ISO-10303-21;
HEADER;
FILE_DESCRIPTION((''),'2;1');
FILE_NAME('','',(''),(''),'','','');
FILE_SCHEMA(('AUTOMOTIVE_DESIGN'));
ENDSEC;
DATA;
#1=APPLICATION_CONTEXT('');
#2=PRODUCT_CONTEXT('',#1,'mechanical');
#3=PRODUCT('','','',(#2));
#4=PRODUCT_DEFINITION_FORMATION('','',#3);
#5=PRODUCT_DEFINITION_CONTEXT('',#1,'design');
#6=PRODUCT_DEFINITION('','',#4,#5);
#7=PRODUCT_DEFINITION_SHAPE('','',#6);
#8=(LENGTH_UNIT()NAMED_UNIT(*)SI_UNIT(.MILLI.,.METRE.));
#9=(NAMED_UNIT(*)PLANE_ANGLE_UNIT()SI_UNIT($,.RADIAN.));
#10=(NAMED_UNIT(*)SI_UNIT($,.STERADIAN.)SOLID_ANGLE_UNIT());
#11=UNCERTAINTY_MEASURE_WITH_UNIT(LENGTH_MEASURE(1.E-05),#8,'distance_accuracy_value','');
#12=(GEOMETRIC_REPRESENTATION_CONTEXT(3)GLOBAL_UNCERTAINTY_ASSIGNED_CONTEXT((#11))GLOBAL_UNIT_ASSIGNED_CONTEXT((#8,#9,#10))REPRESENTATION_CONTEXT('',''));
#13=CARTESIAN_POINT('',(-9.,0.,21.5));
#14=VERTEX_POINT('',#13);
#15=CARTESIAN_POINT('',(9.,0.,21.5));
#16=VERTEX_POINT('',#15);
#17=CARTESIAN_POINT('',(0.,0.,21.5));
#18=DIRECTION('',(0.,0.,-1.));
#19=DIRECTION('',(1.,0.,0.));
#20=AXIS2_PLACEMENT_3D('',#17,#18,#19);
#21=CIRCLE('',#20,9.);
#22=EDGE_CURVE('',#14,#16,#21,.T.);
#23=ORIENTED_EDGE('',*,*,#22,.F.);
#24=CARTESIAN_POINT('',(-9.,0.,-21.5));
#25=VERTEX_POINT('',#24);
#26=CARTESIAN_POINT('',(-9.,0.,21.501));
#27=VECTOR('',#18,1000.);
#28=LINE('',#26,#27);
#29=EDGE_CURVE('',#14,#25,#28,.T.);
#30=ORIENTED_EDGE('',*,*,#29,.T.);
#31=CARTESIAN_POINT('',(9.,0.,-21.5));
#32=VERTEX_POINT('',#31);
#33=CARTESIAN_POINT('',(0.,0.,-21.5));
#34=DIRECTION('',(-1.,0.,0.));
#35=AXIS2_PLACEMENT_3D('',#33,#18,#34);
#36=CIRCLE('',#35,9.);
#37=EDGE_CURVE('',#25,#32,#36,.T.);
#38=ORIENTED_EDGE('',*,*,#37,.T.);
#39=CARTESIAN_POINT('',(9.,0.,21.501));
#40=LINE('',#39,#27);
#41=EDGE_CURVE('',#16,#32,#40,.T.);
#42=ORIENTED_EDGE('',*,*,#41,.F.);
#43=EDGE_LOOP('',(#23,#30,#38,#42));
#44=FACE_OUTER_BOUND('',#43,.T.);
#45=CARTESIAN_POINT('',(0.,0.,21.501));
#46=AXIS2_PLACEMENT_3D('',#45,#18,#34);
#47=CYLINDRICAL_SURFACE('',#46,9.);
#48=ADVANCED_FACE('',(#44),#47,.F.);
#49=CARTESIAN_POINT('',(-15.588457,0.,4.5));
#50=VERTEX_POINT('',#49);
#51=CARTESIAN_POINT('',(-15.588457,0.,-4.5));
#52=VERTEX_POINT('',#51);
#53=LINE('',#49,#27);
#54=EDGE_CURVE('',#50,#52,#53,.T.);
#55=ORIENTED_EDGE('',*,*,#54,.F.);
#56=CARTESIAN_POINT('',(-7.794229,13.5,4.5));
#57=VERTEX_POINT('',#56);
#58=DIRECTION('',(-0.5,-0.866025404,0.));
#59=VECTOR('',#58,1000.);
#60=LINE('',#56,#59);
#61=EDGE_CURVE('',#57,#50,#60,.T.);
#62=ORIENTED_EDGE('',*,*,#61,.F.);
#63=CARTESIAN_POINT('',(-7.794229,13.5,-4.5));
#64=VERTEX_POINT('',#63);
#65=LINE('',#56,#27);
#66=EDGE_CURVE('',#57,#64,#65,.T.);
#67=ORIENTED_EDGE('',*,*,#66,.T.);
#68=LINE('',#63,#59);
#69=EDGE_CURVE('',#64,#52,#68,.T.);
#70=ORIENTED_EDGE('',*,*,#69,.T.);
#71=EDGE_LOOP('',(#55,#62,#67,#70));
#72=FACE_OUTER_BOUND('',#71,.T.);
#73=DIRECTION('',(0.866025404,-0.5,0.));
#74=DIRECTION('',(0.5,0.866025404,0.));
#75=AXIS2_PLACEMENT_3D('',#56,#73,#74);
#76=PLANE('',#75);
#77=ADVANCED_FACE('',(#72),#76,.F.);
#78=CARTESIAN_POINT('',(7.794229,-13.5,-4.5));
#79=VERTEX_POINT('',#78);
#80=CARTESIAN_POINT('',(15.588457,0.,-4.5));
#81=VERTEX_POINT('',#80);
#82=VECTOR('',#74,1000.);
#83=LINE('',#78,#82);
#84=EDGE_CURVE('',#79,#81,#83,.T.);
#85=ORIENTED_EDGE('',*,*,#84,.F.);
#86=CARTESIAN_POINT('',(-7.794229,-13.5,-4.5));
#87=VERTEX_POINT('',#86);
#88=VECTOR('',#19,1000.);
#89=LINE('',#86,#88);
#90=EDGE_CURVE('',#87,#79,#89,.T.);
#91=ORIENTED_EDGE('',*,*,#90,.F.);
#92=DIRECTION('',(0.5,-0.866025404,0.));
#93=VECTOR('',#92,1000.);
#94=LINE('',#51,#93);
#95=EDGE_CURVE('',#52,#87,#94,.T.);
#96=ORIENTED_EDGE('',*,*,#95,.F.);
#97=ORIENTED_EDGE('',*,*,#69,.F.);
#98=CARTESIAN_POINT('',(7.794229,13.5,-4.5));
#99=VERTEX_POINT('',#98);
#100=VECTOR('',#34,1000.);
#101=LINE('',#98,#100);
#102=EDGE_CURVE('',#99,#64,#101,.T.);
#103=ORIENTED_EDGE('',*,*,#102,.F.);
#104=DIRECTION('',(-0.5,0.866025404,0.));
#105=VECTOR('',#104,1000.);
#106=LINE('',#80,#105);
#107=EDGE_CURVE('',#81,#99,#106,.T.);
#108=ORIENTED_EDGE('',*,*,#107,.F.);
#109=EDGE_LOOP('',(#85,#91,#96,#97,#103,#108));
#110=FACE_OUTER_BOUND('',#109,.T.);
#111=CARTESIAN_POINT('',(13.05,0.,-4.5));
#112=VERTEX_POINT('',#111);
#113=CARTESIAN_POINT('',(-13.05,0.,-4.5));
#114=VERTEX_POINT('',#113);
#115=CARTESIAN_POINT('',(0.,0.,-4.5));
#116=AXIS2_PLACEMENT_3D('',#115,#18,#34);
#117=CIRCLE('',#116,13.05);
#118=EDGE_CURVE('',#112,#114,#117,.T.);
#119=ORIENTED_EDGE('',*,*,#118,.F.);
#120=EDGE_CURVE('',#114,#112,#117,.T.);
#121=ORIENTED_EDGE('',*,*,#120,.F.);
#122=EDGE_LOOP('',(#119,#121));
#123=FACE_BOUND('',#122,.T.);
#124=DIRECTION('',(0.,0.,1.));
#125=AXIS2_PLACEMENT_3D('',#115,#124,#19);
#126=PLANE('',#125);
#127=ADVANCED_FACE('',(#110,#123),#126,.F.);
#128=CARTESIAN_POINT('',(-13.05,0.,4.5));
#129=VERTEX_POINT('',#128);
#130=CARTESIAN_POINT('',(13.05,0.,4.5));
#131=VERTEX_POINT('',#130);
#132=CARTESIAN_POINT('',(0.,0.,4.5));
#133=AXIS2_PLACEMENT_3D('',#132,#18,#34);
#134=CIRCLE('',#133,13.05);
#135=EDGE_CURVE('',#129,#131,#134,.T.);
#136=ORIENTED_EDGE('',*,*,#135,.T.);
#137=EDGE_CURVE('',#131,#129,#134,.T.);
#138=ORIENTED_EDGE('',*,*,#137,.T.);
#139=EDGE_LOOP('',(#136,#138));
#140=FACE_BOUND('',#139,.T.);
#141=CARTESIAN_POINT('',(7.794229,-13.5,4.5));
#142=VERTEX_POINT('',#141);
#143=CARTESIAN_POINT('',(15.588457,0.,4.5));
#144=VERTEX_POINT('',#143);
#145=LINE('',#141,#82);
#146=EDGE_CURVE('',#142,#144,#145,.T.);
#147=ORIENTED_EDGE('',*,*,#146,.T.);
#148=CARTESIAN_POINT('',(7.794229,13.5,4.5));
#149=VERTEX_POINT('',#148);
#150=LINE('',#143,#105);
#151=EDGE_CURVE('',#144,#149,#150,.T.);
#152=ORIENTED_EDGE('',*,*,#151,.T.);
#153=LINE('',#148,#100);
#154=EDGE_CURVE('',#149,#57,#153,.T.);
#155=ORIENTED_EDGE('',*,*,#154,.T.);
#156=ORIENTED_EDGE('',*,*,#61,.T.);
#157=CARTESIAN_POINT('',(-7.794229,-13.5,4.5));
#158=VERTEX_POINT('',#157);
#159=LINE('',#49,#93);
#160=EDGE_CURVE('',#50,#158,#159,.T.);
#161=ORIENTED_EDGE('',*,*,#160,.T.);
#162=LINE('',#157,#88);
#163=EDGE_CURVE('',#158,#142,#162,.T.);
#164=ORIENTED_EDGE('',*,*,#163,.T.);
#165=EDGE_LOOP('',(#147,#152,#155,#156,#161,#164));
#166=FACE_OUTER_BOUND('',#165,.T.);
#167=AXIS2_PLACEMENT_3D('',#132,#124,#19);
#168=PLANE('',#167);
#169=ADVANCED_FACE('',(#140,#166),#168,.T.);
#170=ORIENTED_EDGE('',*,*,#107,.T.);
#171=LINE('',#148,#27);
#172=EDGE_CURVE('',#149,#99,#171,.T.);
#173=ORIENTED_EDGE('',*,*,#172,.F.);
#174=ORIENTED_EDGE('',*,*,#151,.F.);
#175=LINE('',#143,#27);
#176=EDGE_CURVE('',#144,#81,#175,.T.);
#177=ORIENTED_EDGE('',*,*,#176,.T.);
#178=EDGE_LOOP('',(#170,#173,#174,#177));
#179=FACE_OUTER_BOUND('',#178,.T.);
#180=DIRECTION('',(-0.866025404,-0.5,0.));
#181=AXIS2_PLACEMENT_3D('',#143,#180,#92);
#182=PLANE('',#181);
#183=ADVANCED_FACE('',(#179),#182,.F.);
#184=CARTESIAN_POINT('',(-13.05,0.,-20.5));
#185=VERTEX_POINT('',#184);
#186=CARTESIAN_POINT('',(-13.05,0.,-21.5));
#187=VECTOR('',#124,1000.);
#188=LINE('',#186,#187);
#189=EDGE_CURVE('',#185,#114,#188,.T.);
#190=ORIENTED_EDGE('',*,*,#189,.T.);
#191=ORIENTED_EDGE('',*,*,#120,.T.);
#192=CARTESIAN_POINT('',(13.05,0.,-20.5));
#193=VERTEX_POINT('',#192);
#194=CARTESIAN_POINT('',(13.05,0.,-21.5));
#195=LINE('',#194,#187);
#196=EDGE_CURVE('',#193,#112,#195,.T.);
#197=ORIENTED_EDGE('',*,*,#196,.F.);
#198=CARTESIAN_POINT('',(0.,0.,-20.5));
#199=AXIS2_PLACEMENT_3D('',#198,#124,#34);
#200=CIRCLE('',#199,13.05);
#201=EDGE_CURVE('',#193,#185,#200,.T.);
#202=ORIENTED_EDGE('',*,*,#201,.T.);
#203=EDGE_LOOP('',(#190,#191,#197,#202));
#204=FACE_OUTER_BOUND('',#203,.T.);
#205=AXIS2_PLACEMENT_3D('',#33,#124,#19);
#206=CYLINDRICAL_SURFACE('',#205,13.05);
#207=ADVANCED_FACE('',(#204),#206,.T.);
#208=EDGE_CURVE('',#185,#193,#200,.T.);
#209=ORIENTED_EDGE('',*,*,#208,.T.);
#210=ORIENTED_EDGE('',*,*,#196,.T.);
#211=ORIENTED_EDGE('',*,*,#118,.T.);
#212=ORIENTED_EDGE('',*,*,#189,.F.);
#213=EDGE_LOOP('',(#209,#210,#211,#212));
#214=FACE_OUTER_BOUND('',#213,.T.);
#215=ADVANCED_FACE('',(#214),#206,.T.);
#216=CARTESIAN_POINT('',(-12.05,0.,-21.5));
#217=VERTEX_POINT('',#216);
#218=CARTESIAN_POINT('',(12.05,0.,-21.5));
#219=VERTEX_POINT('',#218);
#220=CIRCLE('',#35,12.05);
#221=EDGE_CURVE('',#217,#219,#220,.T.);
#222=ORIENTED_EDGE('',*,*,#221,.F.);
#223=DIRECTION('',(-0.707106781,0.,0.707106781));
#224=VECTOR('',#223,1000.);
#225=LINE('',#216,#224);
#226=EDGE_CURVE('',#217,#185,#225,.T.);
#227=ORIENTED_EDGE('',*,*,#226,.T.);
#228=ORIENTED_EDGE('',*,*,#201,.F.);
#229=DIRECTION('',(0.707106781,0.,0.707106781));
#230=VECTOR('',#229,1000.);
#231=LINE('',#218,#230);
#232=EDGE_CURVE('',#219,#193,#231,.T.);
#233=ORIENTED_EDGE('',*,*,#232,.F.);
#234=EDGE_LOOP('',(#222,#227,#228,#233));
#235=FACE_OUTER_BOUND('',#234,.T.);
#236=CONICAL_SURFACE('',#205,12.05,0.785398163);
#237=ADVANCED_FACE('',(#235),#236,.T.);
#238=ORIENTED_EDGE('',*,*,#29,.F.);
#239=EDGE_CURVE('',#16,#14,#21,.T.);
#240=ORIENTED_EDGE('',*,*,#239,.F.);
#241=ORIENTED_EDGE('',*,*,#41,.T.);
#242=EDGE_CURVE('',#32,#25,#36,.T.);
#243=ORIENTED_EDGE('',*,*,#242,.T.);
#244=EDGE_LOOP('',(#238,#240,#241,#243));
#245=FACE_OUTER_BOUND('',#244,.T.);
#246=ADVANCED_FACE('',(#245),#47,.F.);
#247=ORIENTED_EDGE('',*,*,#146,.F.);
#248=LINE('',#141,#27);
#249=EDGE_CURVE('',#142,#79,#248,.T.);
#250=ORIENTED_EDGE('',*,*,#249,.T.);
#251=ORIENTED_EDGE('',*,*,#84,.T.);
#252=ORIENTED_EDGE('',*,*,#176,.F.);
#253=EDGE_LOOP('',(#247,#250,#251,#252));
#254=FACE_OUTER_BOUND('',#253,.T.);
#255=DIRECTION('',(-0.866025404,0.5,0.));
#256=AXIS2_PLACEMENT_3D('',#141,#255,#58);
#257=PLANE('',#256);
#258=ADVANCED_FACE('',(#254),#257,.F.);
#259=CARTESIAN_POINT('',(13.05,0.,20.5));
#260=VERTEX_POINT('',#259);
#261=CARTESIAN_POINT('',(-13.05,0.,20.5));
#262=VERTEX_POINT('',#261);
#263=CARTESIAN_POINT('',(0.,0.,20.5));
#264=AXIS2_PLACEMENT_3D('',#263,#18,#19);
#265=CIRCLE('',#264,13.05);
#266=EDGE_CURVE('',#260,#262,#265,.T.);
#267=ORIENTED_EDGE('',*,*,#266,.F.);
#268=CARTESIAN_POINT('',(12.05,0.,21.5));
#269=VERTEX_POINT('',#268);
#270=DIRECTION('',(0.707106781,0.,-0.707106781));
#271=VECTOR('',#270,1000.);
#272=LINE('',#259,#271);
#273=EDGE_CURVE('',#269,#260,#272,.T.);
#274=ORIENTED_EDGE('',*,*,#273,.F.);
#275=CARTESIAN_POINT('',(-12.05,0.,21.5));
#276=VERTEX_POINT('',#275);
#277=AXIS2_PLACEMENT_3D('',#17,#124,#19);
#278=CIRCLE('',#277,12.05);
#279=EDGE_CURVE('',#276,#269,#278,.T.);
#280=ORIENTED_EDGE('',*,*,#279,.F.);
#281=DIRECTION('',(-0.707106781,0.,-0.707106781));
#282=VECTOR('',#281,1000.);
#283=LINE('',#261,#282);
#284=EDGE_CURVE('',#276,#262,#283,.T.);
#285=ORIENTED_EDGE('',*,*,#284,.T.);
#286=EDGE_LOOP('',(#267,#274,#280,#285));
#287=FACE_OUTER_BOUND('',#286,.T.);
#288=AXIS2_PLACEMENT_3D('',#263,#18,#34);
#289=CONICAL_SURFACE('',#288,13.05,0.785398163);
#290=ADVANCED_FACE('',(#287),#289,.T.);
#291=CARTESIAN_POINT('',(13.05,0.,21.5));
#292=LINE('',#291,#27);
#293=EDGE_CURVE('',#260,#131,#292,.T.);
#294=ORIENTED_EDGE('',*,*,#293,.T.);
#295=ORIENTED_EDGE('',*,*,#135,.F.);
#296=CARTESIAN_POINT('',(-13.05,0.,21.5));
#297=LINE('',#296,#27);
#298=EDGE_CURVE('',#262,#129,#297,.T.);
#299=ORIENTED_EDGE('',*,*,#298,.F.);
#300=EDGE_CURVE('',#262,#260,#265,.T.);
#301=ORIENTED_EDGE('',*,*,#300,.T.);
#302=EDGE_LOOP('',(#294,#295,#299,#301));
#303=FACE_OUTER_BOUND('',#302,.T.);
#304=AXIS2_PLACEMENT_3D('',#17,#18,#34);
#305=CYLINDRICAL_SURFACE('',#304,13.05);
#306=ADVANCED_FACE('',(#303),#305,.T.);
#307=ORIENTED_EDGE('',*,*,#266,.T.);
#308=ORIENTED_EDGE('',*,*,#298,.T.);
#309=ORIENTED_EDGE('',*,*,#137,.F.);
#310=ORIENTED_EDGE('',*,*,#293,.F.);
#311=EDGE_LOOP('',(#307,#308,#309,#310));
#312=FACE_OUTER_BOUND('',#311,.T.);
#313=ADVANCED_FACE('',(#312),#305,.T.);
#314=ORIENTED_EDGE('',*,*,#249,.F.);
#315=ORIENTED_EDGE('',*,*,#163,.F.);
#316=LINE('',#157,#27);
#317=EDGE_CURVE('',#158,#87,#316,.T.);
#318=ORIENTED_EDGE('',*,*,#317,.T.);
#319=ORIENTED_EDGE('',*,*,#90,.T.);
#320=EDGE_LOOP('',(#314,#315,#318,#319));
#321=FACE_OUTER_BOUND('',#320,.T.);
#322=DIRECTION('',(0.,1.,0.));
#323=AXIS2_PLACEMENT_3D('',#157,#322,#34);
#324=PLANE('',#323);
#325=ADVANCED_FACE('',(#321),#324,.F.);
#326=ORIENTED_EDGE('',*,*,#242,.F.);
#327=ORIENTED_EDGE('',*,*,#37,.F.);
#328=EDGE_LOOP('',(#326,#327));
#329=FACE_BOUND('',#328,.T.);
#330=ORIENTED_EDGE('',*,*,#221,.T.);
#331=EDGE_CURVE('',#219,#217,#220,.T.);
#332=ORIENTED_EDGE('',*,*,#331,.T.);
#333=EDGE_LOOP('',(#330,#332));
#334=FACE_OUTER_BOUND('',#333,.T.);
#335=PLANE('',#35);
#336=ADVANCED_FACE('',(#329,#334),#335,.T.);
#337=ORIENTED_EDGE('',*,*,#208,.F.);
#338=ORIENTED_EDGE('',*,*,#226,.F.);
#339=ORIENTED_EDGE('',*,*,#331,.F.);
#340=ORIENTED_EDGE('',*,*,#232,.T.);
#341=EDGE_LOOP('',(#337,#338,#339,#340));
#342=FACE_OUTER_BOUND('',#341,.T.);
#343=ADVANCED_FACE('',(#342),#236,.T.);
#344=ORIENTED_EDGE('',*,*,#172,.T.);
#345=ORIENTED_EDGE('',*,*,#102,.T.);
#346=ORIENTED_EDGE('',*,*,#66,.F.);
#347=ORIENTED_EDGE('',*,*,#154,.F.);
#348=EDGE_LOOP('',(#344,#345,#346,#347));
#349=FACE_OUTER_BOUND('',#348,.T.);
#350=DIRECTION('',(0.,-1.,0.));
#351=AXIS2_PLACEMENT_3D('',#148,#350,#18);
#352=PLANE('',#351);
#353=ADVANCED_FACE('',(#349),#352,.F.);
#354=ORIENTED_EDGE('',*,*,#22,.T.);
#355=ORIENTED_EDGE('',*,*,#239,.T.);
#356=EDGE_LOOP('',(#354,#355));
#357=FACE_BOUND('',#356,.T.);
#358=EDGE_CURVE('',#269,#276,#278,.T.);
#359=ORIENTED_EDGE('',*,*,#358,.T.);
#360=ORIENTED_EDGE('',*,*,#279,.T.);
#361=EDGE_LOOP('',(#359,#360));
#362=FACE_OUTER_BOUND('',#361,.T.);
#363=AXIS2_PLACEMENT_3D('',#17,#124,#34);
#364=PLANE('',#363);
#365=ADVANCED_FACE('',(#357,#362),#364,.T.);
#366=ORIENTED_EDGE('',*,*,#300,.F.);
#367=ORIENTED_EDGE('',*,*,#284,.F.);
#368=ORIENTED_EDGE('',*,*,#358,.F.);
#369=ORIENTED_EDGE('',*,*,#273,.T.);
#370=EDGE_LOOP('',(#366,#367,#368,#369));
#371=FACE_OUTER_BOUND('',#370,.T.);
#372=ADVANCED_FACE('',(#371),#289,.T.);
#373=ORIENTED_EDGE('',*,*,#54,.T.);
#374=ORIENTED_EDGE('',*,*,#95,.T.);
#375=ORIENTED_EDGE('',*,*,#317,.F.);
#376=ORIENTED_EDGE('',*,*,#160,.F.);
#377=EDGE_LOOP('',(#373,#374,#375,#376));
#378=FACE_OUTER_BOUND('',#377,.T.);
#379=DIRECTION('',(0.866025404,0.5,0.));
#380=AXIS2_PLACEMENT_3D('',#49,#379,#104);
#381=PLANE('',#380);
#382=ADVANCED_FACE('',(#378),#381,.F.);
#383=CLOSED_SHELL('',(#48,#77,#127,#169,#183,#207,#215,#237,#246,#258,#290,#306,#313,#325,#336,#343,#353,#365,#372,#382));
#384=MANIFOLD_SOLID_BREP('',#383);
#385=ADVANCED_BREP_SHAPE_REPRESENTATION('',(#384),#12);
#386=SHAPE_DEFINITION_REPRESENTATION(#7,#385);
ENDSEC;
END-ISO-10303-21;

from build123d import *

# Parameters (mm, degrees)
EXTRUDE_1_DEPTH     = 4.5
SKETCH_4_R          = 13.05
EXTRUDE_3_DEPTH     = 17
CUT_EXTRUDE_2_REACH = 49.689
SKETCH_5_R          = 9
CHAMFER_1_SIZE      = 1


with BuildPart() as part:
    # 草图1 → 凸台-拉伸1 (new, symmetric)
    with BuildSketch(Plane.XY):
        Polygon((15.588457268, 0), (7.794228634, 13.5), (-7.794228634, 13.5), (-15.588457268, 0), (-7.794228634, -13.5), (7.794228634, -13.5), align=None)
    extrude(amount=EXTRUDE_1_DEPTH, both=True)

    # 草图4 → 凸台-拉伸3 (add)
    with BuildSketch(Plane(origin=(0, 0, -4.5), x_dir=(-1, 0, 0), z_dir=(0, 0, -1))):
        Circle(SKETCH_4_R)
    extrude_3 = extrude(amount=EXTRUDE_3_DEPTH)

    # 镜向1: 凸台-拉伸3 across plane
    add(extrude_3.mirror(Plane.XY))

    # 草图5 → 切除-拉伸2 (cut, up to next)
    with BuildSketch(Plane(origin=(0, 0, -21.5), x_dir=(-1, 0, 0), z_dir=(0, 0, -1)), mode=Mode.PRIVATE) as cut_extrude_2_sk1:
        Circle(SKETCH_5_R)
    cut_extrude_2_tool1 = extrude(cut_extrude_2_sk1.sketch, amount=-CUT_EXTRUDE_2_REACH, mode=Mode.PRIVATE) & part.part
    add(cut_extrude_2_tool1.solids().sort_by_distance((0, 0, -21.5))[0], mode=Mode.SUBTRACT)

    # 倒角1
    chamfer_1_edges = [part.edges().sort_by_distance(p)[0] for p in [
        (13.05, 0, -21.5),
        (13.05, 0, 21.5),
    ]]
    chamfer(chamfer_1_edges, length=CHAMFER_1_SIZE)


solid = part.part
